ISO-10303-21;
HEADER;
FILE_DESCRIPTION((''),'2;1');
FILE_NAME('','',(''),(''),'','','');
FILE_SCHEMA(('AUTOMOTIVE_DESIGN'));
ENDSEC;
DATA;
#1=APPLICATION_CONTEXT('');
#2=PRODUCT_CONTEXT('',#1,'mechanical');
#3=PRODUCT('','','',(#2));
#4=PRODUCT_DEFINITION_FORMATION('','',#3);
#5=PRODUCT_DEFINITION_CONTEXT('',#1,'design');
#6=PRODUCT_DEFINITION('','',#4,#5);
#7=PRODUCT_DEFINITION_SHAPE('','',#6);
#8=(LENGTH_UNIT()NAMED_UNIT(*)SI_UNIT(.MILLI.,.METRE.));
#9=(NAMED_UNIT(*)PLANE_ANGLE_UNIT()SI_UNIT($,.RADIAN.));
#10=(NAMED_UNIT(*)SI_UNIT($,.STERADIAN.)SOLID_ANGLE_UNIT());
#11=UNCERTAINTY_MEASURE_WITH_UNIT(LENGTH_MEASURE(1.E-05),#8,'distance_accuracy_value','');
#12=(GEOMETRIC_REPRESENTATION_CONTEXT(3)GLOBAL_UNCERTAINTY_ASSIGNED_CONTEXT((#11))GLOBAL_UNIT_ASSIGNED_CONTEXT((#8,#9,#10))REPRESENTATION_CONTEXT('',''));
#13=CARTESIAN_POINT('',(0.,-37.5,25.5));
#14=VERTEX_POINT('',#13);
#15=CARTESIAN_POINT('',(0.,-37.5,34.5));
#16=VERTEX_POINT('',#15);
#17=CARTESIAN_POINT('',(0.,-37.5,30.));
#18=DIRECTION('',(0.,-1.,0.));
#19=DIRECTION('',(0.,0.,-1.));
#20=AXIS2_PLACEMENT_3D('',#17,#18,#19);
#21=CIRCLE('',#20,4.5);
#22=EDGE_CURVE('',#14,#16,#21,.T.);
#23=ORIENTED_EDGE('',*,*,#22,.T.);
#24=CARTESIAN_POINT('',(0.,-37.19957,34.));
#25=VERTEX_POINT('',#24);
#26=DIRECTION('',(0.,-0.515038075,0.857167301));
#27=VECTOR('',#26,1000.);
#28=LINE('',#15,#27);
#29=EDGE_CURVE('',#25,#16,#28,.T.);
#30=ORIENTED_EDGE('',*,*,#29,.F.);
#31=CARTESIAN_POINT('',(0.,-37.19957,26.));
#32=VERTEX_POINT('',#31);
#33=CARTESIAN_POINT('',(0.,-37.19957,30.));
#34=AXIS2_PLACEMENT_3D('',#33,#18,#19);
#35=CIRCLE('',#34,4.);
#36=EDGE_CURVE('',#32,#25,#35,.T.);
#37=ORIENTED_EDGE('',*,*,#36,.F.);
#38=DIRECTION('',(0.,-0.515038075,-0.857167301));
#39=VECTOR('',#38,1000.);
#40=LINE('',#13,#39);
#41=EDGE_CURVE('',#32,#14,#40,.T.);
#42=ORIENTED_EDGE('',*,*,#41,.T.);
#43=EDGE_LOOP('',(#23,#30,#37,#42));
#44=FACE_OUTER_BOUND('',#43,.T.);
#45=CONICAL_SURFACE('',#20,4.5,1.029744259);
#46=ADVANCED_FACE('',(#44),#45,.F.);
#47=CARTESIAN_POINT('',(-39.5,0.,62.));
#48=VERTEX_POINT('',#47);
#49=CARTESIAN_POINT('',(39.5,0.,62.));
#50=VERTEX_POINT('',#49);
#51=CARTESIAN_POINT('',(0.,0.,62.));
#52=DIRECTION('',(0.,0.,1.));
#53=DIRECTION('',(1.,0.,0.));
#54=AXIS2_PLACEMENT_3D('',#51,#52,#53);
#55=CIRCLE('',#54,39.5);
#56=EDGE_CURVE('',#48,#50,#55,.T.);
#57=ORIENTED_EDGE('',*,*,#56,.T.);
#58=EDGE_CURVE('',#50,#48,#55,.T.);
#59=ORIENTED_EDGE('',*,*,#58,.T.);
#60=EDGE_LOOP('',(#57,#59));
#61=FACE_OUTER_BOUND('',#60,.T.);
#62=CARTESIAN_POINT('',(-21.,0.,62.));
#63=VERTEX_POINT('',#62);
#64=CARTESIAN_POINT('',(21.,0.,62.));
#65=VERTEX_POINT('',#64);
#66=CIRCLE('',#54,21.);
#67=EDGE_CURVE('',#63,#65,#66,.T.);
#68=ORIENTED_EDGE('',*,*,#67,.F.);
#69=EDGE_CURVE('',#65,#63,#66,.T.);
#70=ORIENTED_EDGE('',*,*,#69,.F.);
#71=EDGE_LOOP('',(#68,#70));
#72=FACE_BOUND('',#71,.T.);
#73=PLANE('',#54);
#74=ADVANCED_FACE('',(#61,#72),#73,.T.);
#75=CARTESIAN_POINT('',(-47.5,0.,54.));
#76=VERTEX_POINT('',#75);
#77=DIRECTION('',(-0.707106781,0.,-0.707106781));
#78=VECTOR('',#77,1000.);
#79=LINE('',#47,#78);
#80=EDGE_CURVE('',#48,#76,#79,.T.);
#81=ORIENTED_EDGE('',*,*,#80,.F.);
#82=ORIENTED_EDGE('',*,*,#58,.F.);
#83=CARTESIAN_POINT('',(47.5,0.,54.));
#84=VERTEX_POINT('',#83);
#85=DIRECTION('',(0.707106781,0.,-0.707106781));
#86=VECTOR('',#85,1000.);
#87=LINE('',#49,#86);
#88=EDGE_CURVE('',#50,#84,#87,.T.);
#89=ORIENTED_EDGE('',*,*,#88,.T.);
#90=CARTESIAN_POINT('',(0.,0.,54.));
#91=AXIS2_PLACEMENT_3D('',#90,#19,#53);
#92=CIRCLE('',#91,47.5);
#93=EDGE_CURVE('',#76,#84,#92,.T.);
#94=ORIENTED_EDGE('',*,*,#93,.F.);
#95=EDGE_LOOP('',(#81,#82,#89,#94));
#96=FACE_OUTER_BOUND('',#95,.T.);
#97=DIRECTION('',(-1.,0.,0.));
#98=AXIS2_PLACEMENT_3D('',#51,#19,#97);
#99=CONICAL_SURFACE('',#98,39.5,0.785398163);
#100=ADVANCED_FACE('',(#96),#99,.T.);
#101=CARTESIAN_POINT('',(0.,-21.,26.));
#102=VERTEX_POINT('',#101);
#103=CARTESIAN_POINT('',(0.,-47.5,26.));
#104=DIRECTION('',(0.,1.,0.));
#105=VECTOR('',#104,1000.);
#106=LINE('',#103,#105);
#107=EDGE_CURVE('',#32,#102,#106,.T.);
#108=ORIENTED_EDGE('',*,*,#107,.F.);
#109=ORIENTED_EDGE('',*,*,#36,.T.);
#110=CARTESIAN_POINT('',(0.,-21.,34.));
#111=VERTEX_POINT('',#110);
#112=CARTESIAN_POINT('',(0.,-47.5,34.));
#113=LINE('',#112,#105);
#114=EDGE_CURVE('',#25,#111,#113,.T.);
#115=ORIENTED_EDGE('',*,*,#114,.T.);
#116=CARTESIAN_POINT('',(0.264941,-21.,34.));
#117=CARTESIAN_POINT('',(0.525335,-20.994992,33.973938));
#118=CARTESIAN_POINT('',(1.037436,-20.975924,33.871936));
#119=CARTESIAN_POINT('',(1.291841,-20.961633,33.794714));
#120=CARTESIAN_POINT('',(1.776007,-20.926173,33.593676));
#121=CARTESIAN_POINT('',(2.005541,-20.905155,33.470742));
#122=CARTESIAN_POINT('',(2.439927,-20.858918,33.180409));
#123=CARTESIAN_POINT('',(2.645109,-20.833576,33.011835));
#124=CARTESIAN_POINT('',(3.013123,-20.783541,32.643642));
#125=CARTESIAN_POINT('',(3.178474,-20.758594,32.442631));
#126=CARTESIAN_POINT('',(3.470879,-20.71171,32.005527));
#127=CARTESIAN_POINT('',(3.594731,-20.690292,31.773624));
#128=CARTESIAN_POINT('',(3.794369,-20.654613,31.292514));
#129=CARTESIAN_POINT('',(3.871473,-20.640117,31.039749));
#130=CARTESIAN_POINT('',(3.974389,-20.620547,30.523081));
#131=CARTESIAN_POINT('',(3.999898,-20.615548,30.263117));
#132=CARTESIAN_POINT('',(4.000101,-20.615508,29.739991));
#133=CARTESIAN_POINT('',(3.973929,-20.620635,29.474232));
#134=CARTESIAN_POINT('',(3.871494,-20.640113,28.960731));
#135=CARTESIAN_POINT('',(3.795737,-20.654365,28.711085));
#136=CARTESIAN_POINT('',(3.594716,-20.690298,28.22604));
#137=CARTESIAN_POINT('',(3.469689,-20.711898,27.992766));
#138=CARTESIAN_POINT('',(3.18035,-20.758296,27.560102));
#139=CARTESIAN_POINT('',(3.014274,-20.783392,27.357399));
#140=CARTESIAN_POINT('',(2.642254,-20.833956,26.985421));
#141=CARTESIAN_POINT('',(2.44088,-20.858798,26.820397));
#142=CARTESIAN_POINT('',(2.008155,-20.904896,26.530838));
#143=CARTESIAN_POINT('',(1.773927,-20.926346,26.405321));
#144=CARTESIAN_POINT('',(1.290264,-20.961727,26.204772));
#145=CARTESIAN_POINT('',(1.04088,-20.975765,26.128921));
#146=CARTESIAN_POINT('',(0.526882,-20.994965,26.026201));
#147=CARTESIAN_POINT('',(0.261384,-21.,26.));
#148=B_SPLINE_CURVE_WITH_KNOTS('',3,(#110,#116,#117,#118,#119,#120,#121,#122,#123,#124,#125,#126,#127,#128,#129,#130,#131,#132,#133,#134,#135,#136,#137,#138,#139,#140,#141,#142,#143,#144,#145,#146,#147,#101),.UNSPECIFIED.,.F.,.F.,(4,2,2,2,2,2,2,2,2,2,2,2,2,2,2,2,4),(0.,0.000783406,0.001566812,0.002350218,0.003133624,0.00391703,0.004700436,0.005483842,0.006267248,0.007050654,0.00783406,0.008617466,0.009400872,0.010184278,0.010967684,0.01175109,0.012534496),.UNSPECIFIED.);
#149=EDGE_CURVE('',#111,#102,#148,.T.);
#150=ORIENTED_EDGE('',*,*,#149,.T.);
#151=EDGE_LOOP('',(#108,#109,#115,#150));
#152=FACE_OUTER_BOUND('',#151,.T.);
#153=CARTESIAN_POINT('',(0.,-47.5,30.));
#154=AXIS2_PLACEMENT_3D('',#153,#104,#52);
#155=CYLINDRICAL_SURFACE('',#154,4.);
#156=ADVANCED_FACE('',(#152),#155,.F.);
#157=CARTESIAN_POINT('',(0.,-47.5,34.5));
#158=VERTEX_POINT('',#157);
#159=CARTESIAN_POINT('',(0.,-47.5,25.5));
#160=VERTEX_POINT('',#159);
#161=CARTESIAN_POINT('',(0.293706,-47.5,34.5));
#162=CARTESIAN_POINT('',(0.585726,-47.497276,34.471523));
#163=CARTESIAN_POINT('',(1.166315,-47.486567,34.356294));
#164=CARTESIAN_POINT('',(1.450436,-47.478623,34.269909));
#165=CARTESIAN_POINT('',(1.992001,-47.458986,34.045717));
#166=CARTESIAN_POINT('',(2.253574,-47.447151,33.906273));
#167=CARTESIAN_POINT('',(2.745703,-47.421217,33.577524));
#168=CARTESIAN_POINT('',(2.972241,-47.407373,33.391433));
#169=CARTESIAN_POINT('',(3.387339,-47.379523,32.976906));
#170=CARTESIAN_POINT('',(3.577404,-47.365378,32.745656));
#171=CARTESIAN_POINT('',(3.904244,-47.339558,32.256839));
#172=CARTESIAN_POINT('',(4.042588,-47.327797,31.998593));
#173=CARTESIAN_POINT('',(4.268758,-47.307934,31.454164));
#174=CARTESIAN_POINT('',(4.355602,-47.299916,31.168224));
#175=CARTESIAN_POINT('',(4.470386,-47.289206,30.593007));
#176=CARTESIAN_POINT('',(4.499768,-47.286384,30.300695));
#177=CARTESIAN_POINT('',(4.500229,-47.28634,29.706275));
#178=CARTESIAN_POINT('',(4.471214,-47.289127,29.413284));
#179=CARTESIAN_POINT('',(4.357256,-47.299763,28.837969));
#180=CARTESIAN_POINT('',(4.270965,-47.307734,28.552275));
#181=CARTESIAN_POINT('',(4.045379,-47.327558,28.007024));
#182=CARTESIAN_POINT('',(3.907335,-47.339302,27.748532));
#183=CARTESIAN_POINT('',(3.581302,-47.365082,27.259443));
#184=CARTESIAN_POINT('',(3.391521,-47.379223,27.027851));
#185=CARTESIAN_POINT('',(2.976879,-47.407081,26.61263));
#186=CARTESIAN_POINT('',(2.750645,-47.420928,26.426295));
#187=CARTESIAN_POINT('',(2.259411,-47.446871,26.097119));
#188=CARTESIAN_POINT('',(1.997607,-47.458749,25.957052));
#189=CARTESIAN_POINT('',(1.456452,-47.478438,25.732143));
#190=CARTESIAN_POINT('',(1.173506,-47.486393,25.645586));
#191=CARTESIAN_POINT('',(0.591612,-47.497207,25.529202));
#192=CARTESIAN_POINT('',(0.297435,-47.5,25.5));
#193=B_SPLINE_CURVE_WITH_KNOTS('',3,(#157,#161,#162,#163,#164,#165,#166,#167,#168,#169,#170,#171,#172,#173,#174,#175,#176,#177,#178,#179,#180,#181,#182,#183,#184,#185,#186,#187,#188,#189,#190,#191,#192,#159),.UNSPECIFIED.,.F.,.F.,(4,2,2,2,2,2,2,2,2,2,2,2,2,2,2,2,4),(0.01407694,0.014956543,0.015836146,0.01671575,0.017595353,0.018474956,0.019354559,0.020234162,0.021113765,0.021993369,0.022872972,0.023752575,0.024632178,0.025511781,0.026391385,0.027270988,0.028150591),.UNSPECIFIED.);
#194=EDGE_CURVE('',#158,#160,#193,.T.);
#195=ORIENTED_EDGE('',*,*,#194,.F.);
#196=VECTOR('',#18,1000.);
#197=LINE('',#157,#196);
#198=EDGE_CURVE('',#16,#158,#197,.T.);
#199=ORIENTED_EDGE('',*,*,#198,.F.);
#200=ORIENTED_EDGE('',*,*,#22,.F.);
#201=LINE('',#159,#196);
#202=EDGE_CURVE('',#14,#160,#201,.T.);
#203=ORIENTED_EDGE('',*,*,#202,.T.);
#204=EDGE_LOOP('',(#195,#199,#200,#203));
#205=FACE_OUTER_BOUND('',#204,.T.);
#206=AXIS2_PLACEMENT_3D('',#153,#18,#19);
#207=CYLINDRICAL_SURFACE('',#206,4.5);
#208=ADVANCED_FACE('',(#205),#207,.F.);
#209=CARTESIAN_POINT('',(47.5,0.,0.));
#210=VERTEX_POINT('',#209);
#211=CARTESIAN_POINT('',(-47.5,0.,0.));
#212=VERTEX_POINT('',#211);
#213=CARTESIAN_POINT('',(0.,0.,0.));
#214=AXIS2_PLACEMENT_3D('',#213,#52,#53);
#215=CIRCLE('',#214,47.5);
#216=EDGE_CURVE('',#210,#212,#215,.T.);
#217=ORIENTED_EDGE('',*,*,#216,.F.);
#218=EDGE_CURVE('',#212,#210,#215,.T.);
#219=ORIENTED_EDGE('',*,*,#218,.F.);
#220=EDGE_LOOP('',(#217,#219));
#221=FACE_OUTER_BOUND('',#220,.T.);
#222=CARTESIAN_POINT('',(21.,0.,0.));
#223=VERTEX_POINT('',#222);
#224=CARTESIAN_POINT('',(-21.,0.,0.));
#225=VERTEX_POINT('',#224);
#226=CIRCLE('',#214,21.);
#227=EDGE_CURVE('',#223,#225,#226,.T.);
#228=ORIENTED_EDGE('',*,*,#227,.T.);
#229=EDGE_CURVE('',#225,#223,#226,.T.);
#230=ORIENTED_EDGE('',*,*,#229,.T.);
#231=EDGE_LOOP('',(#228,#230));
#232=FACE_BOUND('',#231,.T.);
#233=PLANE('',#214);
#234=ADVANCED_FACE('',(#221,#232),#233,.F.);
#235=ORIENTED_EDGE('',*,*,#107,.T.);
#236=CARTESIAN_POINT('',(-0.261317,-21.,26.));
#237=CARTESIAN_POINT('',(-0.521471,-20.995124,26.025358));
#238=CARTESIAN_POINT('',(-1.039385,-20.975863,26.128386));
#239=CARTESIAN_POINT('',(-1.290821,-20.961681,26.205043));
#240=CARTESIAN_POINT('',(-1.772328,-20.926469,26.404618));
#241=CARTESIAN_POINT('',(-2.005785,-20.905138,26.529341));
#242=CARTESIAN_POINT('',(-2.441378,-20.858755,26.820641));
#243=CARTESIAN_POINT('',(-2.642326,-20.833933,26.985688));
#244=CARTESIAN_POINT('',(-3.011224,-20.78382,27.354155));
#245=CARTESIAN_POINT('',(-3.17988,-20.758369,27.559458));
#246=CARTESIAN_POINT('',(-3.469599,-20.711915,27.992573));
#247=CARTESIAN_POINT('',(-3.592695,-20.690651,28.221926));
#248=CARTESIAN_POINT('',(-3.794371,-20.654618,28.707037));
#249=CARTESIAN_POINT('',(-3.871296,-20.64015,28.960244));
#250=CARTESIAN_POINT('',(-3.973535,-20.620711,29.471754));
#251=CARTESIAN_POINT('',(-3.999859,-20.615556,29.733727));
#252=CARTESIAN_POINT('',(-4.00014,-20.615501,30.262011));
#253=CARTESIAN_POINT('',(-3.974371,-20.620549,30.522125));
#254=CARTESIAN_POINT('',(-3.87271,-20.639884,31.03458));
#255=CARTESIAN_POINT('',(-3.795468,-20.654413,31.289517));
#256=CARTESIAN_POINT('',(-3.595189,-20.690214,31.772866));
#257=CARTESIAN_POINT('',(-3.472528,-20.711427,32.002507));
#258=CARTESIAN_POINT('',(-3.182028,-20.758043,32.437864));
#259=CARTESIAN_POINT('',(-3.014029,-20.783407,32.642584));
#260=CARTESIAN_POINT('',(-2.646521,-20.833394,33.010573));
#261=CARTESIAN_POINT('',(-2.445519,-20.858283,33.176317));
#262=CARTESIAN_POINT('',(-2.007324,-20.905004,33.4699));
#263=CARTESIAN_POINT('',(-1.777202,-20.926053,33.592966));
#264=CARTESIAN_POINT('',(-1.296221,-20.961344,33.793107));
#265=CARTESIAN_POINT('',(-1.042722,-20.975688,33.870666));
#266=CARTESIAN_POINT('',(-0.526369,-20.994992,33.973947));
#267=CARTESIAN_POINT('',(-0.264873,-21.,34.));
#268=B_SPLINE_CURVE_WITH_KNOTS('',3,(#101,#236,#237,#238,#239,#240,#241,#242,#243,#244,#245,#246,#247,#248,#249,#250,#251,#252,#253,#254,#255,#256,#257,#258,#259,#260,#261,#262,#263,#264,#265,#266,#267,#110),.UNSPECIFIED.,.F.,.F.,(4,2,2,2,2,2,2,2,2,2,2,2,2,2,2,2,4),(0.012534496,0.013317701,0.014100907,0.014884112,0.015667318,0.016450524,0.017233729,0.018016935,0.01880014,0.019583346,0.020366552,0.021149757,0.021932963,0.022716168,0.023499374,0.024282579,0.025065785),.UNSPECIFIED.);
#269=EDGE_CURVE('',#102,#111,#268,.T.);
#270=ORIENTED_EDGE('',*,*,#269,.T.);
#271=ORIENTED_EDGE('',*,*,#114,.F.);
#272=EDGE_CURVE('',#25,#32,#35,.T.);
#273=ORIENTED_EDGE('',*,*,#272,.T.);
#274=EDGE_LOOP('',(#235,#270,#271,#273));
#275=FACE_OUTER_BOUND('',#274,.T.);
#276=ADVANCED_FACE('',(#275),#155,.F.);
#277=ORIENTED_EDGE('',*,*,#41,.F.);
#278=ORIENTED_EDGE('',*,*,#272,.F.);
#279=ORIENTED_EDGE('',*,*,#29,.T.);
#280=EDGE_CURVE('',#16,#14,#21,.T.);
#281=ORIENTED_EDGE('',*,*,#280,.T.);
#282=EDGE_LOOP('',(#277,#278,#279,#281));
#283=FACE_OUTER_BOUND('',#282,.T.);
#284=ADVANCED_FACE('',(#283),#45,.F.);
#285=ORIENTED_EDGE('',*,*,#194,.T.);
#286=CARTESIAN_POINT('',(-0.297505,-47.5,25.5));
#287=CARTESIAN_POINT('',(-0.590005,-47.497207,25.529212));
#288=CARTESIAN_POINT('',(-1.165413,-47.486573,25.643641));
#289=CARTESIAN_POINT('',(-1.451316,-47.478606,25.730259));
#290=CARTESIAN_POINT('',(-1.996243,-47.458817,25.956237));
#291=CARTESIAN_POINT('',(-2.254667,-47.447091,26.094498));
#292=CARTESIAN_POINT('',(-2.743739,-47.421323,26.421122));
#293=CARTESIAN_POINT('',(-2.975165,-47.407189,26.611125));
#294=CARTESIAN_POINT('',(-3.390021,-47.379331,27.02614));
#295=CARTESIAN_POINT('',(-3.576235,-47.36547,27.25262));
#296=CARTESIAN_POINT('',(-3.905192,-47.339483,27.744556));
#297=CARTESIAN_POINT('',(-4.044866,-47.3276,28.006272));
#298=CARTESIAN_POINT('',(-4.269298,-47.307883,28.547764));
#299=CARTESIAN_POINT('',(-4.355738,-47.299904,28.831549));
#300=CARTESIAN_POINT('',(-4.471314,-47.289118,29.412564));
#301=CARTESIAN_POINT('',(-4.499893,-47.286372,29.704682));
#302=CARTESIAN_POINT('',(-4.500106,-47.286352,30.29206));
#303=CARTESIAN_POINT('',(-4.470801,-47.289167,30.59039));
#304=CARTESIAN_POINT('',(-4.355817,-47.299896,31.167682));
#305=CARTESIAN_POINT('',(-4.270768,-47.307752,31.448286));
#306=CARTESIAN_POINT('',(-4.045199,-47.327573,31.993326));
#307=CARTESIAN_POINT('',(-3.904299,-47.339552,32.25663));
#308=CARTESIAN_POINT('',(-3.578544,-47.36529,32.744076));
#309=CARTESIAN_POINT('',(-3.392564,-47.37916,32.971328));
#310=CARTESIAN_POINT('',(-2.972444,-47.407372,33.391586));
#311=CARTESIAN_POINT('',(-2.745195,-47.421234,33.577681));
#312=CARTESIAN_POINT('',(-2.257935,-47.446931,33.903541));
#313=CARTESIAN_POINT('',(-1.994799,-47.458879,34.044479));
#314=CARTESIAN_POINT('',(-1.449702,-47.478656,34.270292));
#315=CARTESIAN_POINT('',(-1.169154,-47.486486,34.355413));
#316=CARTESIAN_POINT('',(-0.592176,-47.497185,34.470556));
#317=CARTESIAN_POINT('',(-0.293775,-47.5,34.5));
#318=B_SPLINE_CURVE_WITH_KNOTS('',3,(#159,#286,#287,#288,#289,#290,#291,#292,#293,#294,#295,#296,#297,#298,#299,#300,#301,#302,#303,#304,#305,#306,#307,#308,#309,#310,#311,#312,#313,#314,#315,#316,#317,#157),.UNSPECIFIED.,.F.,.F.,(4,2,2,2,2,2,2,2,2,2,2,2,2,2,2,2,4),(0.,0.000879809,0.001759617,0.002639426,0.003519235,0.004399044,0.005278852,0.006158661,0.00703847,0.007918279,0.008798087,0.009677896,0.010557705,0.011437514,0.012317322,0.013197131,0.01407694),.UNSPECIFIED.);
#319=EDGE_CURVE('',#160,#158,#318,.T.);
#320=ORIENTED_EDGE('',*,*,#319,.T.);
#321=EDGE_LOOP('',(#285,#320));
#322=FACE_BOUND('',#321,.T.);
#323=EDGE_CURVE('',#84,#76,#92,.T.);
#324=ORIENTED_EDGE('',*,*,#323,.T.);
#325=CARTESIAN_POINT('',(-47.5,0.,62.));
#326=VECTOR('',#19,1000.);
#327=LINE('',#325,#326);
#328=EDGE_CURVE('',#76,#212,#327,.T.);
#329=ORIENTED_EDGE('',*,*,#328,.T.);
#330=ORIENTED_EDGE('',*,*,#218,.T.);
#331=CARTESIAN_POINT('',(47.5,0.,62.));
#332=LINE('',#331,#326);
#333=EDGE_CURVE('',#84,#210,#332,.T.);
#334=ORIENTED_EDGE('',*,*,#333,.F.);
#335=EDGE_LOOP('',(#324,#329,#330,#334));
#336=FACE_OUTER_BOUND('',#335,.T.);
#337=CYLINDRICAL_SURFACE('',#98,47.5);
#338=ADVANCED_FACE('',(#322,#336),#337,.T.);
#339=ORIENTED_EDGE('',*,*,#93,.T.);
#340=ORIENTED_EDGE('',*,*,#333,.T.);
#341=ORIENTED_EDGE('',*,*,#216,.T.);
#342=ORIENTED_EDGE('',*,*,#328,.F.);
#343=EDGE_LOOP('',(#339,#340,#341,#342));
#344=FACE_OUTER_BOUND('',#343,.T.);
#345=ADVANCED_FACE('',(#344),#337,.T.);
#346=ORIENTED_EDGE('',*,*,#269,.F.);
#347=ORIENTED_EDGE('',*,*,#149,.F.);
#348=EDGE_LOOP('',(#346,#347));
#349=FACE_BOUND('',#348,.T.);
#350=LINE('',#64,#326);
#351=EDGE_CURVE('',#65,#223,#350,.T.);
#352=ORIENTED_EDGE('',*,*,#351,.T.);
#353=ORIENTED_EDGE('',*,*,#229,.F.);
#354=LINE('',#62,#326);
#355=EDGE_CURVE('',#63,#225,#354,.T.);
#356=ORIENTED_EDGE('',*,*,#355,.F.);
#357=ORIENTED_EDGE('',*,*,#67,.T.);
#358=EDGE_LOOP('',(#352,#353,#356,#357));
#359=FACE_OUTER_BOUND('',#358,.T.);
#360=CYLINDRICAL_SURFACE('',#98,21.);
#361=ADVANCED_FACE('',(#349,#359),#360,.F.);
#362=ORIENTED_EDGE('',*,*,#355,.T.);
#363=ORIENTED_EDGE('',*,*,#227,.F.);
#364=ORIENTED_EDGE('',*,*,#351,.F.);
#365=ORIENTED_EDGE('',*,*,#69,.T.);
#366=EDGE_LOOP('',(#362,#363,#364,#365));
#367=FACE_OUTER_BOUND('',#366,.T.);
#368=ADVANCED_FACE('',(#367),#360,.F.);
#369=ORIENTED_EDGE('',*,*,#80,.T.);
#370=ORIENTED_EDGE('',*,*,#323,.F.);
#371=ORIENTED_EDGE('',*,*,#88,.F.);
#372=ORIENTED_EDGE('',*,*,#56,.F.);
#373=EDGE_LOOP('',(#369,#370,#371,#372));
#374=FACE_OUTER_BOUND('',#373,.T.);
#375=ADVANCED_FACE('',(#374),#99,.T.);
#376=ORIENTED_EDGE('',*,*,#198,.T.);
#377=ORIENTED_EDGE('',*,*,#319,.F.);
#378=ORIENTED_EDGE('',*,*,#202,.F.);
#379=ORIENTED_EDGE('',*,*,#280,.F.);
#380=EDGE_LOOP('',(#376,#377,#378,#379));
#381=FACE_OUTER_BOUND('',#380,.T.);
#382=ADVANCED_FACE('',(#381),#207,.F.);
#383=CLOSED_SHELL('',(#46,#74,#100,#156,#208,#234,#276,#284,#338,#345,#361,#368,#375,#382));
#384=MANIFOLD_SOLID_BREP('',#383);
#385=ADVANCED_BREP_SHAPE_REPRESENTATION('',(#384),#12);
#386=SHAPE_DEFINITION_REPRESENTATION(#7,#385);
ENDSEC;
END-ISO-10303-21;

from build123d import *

# Parameters (mm, degrees)
SKETCH_1_R          = 47.5
SKETCH_1_R_2        = 21
EXTRUDE_1_DEPTH     = 62
CHAMFER_1_SIZE      = 8
SKETCH_2_R          = 4
CUT_EXTRUDE_1_DEPTH = 92.413893911
M10X1_0_1_D         = 9
M10X1_0_1_DEPTH     = 10
M10X1_0_1_TIP       = 2.703872786


with BuildPart() as part:
    # 草图1 → 凸台-拉伸1 (new body)
    with BuildSketch(Plane.XY):
        Circle(SKETCH_1_R)
        Circle(SKETCH_1_R_2, mode=Mode.SUBTRACT)
    extrude(amount=EXTRUDE_1_DEPTH)

    # 倒角1
    chamfer_1_edges = [part.edges().sort_by_distance(p)[0] for p in [
        (-47.5, 0, 62),
    ]]
    chamfer(chamfer_1_edges, length=CHAMFER_1_SIZE)

    # 草图2 → 切除-拉伸1 (cut, through all)
    with BuildSketch(Plane(origin=(0, 0, 0), x_dir=(1, 0, 0), z_dir=(0, 1, 0))):
        with Locations(Location((0, -30, 0), (0, 0, 270))):
            Circle(SKETCH_2_R)
    extrude(amount=-CUT_EXTRUDE_1_DEPTH, mode=Mode.SUBTRACT)

    # M10x1.0 螺纹孔1
    with Locations(Plane.XZ.offset(47.5)):
        with Locations((0, 30)):
            Hole(M10X1_0_1_D / 2, depth=M10X1_0_1_DEPTH)
            with Locations((0, 0, -(M10X1_0_1_DEPTH + M10X1_0_1_TIP / 2))):  # 118° drill point
                Cone(0, M10X1_0_1_D / 2, M10X1_0_1_TIP, mode=Mode.SUBTRACT)


solid = part.part
